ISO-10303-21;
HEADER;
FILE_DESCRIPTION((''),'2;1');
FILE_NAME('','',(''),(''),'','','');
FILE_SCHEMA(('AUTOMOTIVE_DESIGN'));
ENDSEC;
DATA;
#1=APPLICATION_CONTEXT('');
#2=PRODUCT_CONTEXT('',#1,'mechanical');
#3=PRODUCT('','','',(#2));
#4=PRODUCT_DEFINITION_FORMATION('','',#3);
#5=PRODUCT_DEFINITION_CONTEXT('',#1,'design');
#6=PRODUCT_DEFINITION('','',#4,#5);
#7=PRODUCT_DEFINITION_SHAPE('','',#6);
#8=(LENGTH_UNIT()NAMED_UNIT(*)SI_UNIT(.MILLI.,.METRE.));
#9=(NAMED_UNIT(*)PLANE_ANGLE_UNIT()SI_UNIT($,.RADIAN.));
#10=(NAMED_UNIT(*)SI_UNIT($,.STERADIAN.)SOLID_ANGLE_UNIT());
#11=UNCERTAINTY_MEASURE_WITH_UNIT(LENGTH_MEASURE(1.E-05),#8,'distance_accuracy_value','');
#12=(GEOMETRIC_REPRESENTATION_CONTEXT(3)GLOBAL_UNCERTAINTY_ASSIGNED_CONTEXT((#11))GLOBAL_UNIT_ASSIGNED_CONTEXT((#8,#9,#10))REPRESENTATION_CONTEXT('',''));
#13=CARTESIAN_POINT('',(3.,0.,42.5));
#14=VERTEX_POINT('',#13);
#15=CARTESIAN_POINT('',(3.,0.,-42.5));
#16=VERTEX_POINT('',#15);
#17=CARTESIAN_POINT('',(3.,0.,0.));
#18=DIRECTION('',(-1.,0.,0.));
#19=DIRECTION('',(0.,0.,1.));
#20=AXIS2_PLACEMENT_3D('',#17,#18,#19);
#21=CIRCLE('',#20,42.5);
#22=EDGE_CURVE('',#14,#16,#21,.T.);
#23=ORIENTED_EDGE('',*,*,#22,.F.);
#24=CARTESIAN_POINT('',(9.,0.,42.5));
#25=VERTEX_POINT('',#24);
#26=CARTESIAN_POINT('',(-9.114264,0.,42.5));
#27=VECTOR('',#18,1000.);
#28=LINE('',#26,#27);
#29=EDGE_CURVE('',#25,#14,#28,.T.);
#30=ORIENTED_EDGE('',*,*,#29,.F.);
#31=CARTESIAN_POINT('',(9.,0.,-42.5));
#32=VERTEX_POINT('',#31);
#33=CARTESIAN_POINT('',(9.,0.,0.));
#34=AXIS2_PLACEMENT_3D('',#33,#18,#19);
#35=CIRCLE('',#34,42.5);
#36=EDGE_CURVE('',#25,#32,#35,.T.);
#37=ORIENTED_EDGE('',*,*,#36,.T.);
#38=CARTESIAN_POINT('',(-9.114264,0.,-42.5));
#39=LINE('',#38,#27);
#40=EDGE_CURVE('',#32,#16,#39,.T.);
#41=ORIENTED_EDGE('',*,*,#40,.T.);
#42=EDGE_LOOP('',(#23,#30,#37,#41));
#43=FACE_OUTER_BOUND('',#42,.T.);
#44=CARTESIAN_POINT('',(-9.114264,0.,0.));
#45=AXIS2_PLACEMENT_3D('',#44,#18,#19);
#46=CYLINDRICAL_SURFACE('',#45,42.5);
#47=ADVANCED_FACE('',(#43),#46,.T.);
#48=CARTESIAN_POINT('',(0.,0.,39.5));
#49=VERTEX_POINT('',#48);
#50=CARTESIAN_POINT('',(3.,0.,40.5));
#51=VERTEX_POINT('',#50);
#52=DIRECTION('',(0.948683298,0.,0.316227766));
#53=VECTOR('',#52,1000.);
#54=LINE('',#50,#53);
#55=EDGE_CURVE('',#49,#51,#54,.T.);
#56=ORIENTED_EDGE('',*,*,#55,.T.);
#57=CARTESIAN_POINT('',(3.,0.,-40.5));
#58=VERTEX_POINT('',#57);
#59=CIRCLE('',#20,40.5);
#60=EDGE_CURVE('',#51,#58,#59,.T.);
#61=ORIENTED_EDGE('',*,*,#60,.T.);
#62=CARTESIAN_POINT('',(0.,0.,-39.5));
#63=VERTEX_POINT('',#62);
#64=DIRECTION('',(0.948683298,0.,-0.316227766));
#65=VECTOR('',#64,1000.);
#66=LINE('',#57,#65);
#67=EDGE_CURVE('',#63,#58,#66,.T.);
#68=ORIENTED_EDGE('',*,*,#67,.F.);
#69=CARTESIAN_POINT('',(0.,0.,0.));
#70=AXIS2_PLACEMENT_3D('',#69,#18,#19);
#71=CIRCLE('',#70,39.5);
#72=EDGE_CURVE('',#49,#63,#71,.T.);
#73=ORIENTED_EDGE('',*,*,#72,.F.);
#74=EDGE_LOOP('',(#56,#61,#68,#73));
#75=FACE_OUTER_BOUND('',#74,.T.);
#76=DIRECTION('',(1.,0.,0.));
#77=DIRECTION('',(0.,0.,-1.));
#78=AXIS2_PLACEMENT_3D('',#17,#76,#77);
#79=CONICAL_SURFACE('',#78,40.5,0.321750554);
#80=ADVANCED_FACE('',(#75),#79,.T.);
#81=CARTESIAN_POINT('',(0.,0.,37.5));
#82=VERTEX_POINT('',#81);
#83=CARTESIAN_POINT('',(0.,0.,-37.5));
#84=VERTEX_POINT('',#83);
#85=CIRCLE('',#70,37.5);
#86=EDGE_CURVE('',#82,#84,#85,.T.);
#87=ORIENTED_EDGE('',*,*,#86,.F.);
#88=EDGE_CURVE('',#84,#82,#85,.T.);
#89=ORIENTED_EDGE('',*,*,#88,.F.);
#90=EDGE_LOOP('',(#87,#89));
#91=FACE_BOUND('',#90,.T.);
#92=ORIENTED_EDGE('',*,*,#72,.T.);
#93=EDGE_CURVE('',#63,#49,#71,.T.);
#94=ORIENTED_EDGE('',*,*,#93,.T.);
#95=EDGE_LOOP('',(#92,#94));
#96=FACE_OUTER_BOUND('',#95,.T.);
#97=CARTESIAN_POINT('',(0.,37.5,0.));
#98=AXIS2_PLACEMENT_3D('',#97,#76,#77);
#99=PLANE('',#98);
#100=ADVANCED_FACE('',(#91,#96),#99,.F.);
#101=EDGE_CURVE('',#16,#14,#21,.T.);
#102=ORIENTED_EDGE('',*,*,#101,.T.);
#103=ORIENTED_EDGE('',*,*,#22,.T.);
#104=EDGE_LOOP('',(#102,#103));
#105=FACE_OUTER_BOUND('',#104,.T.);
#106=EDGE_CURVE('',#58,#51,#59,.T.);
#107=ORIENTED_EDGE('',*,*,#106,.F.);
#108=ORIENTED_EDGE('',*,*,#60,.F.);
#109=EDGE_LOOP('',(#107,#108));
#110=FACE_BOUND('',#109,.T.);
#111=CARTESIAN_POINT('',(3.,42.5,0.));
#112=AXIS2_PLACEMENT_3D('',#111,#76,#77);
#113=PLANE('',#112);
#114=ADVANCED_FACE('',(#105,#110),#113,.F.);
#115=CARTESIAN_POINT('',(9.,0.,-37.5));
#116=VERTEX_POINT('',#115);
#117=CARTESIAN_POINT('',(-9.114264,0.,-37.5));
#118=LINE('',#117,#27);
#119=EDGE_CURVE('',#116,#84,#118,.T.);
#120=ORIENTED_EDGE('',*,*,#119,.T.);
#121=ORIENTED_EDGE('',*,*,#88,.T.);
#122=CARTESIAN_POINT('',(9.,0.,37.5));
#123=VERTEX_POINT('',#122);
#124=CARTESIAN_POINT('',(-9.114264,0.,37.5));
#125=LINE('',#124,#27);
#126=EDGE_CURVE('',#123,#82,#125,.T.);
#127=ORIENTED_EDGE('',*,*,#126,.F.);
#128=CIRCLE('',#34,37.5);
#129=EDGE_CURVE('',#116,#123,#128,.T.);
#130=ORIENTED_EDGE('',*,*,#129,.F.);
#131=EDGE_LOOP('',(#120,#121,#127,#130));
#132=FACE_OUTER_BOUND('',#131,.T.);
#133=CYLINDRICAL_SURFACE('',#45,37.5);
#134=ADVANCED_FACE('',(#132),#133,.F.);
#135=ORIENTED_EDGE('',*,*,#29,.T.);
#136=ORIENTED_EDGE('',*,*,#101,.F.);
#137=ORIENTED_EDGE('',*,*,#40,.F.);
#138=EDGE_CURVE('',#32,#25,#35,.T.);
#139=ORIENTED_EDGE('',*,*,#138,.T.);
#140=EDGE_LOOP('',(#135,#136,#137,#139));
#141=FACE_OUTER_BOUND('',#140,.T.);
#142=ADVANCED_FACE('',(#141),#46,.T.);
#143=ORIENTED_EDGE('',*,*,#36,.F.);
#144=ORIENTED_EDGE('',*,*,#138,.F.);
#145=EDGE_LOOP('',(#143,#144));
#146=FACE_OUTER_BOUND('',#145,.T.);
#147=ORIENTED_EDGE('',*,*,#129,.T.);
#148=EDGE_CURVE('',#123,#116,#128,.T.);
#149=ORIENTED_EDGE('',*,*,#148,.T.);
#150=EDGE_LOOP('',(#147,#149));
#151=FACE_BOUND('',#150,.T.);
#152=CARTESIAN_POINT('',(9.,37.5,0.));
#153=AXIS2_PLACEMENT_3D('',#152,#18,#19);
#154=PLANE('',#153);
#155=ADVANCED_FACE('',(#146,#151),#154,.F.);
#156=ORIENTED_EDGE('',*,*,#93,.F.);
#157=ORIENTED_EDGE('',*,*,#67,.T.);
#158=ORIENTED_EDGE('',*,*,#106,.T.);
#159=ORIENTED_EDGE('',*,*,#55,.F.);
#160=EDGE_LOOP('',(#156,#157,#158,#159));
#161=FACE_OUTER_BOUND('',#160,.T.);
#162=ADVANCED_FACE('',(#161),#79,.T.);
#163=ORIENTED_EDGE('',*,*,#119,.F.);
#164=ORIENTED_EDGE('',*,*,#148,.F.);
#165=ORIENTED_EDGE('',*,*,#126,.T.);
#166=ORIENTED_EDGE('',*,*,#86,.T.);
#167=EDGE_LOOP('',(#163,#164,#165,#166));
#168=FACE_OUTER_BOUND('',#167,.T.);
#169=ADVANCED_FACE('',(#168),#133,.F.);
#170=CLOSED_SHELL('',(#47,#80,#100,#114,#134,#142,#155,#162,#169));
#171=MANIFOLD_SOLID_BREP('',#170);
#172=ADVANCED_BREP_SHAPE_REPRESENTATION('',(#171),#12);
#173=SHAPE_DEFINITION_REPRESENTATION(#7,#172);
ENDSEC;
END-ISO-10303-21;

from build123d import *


with BuildPart() as part:
    # 草图1 → 旋转1 (revolve)
    with BuildSketch(Plane.XY, mode=Mode.PRIVATE) as revolve_1_sk:
        Polygon((0, 37.5), (9, 37.5), (9, 42.5), (3, 42.5), (3, 40.5), (0, 39.5), align=None)
    revolve(revolve_1_sk.sketch.rotate(Axis((-9.114263851, 0, 0), (1, 0, 0)), 90), axis=Axis((-9.114263851, 0, 0), (1, 0, 0)))


solid = part.part
